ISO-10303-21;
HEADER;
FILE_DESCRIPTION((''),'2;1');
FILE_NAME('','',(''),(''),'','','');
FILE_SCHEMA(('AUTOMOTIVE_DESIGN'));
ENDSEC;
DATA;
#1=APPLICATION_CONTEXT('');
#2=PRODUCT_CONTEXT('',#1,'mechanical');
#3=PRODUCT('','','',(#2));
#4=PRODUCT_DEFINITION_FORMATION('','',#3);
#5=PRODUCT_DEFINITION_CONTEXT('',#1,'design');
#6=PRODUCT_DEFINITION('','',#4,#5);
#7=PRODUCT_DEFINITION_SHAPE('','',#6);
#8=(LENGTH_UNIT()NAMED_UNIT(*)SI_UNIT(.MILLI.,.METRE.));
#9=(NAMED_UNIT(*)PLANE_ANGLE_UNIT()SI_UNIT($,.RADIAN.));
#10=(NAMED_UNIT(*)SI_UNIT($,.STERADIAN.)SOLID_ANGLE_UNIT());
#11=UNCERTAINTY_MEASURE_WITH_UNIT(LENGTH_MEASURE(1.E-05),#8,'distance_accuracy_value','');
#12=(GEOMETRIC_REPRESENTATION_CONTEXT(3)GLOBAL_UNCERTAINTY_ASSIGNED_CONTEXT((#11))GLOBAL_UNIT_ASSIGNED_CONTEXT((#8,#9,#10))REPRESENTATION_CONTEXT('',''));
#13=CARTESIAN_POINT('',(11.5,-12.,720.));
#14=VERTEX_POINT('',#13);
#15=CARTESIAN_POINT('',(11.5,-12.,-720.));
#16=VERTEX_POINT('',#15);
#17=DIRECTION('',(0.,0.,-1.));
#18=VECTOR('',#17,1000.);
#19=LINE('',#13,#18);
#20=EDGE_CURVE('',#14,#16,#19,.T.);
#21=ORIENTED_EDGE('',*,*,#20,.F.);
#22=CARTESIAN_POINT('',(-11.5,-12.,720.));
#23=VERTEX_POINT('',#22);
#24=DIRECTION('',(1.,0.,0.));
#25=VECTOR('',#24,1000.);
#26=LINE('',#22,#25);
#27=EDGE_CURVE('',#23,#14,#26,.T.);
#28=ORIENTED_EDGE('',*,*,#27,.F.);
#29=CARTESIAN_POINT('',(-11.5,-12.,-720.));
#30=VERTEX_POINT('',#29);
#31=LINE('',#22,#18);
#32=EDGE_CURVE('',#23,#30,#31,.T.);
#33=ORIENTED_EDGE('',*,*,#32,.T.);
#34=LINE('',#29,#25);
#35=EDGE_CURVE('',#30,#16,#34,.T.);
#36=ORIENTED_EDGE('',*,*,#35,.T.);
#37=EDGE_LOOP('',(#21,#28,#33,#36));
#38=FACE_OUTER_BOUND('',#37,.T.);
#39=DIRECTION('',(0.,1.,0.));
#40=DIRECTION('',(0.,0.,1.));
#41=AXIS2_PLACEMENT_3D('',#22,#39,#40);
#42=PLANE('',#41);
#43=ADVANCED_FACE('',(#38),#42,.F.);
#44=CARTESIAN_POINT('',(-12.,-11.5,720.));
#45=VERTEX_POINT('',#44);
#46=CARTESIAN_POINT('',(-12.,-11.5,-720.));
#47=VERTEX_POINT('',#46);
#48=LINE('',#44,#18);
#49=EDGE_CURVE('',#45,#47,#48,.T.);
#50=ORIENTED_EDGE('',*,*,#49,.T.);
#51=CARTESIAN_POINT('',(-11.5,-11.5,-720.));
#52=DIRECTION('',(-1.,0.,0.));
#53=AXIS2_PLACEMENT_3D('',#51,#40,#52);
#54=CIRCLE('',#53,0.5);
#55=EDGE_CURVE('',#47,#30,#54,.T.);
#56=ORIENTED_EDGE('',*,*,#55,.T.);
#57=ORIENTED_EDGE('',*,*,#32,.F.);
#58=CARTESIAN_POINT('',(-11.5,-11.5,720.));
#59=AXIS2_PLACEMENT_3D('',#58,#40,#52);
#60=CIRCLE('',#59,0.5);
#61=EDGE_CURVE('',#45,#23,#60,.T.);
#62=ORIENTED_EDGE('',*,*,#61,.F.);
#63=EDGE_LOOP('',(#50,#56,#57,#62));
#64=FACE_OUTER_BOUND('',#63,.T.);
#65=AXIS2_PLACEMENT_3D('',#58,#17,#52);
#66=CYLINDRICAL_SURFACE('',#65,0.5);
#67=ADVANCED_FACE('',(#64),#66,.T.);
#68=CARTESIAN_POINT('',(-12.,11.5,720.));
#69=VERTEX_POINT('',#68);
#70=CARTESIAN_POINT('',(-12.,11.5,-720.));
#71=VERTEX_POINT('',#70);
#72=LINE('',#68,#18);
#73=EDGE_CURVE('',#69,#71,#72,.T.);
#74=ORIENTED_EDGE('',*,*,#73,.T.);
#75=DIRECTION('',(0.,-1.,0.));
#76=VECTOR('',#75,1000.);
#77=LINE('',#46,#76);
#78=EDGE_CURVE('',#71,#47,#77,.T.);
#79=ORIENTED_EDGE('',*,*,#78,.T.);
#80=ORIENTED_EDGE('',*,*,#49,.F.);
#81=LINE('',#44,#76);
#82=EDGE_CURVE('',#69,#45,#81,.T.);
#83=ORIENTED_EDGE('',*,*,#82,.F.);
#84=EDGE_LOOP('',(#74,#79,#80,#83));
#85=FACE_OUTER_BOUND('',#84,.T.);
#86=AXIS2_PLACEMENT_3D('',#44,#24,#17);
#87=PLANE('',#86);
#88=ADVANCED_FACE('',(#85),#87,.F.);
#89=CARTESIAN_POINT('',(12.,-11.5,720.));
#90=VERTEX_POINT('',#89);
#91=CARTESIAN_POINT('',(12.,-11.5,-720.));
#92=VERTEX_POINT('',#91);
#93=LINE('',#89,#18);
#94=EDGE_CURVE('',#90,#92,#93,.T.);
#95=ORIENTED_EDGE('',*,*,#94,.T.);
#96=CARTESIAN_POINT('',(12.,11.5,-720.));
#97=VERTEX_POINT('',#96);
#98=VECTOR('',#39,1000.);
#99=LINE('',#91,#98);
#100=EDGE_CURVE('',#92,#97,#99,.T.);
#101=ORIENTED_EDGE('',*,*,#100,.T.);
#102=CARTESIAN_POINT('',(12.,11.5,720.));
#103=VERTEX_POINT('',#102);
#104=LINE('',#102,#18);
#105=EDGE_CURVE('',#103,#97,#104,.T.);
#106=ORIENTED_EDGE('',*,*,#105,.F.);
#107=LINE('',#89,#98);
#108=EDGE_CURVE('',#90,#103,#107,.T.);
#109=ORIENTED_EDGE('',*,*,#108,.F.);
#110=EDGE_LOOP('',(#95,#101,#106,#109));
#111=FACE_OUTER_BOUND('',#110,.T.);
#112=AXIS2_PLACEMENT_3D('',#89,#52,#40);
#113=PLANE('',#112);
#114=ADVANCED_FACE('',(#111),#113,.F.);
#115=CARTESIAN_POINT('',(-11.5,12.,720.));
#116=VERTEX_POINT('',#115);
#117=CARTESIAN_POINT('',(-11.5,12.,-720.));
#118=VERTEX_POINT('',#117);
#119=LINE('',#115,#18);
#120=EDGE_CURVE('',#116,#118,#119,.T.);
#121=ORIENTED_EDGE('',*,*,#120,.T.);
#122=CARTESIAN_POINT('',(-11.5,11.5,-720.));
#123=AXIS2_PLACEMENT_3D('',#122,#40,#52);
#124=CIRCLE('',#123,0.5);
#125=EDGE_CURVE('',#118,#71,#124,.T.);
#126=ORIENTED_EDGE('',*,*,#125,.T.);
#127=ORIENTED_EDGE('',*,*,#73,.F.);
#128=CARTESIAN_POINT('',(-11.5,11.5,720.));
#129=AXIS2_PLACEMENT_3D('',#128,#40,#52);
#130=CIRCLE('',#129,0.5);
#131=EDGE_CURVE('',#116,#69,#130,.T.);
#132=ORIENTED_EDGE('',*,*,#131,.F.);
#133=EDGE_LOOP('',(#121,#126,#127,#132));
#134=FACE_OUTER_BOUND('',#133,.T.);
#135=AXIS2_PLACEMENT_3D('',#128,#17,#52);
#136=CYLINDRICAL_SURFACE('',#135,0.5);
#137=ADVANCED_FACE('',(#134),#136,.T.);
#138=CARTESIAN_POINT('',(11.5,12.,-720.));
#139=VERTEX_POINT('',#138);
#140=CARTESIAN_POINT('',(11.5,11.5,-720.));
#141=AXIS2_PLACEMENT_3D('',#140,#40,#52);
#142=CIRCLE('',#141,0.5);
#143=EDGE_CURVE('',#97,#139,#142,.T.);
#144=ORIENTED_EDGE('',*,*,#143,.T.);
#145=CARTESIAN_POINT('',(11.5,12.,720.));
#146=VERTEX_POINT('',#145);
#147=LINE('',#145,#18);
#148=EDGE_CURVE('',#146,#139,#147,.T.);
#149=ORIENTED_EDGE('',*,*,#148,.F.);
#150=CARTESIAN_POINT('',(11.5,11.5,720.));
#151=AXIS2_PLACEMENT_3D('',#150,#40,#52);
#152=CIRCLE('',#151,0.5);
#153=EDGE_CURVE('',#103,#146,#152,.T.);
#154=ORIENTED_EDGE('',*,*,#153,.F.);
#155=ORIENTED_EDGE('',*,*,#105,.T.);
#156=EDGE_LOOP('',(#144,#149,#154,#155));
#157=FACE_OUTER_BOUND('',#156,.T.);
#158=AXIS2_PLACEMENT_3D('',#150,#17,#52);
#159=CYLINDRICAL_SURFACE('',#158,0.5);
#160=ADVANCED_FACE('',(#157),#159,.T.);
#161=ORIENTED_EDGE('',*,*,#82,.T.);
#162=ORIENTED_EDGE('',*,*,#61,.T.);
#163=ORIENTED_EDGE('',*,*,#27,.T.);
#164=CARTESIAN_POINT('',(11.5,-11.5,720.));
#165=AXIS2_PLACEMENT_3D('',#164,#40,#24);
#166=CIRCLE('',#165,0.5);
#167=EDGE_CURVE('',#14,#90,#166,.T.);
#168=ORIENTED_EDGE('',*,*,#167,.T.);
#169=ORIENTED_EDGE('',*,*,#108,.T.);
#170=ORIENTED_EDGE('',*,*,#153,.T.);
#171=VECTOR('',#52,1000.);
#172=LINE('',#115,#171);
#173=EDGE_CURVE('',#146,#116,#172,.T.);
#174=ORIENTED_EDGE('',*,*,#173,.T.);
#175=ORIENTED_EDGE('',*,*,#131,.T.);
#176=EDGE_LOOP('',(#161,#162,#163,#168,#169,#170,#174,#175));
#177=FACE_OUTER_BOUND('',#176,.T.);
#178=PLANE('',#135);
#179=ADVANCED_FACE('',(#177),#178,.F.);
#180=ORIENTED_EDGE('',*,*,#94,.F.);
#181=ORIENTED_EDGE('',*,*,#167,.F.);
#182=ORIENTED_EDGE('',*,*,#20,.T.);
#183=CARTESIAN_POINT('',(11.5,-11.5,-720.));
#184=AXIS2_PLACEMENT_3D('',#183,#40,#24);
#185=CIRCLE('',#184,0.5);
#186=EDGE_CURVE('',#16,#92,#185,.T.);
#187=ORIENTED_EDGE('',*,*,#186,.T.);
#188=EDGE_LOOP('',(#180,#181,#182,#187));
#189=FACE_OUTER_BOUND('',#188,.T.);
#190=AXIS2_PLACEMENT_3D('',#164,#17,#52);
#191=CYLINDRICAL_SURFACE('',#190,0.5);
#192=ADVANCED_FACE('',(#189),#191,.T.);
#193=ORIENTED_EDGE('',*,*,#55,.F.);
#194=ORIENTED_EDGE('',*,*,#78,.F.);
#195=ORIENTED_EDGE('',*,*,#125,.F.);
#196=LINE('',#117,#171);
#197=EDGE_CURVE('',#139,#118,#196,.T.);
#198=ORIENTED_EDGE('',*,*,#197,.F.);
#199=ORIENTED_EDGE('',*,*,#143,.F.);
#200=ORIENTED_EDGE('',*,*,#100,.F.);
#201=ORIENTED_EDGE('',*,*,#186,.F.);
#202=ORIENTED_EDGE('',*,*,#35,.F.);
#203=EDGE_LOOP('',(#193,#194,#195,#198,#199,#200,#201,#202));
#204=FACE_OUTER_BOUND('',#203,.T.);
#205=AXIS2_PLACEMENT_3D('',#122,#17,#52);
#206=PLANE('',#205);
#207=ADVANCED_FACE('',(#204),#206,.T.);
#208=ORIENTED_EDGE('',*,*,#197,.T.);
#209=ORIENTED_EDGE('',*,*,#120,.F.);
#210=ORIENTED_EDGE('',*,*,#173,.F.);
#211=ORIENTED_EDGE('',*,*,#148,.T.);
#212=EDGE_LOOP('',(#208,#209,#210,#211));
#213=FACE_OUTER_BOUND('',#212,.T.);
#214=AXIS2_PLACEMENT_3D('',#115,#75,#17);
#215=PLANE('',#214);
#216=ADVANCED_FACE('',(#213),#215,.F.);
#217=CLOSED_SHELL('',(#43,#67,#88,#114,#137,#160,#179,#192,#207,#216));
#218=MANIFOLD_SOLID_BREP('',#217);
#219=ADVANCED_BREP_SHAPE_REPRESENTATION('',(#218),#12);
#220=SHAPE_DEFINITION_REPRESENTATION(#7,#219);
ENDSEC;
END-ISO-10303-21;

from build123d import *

# Parameters (mm, degrees)
BOSS_EXTRUDE1_DEPTH = 720


with BuildPart() as part:
    # Sketch1 → Boss-Extrude1 (new, symmetric)
    with BuildSketch(Plane.XY):
        with BuildLine():
            Line((-11.5, -12), (11.5, -12))
            ThreePointArc((11.5, -12), (11.853553391, -11.853553391), (12, -11.5))
            Line((12, -11.5), (12, 11.5))
            ThreePointArc((12, 11.5), (11.853553391, 11.853553391), (11.5, 12))
            Line((11.5, 12), (-11.5, 12))
            ThreePointArc((-11.5, 12), (-11.853553391, 11.853553391), (-12, 11.5))
            Line((-12, 11.5), (-12, -11.5))
            ThreePointArc((-12, -11.5), (-11.853553391, -11.853553391), (-11.5, -12))
        make_face()
    extrude(amount=BOSS_EXTRUDE1_DEPTH, both=True)


solid = part.part
